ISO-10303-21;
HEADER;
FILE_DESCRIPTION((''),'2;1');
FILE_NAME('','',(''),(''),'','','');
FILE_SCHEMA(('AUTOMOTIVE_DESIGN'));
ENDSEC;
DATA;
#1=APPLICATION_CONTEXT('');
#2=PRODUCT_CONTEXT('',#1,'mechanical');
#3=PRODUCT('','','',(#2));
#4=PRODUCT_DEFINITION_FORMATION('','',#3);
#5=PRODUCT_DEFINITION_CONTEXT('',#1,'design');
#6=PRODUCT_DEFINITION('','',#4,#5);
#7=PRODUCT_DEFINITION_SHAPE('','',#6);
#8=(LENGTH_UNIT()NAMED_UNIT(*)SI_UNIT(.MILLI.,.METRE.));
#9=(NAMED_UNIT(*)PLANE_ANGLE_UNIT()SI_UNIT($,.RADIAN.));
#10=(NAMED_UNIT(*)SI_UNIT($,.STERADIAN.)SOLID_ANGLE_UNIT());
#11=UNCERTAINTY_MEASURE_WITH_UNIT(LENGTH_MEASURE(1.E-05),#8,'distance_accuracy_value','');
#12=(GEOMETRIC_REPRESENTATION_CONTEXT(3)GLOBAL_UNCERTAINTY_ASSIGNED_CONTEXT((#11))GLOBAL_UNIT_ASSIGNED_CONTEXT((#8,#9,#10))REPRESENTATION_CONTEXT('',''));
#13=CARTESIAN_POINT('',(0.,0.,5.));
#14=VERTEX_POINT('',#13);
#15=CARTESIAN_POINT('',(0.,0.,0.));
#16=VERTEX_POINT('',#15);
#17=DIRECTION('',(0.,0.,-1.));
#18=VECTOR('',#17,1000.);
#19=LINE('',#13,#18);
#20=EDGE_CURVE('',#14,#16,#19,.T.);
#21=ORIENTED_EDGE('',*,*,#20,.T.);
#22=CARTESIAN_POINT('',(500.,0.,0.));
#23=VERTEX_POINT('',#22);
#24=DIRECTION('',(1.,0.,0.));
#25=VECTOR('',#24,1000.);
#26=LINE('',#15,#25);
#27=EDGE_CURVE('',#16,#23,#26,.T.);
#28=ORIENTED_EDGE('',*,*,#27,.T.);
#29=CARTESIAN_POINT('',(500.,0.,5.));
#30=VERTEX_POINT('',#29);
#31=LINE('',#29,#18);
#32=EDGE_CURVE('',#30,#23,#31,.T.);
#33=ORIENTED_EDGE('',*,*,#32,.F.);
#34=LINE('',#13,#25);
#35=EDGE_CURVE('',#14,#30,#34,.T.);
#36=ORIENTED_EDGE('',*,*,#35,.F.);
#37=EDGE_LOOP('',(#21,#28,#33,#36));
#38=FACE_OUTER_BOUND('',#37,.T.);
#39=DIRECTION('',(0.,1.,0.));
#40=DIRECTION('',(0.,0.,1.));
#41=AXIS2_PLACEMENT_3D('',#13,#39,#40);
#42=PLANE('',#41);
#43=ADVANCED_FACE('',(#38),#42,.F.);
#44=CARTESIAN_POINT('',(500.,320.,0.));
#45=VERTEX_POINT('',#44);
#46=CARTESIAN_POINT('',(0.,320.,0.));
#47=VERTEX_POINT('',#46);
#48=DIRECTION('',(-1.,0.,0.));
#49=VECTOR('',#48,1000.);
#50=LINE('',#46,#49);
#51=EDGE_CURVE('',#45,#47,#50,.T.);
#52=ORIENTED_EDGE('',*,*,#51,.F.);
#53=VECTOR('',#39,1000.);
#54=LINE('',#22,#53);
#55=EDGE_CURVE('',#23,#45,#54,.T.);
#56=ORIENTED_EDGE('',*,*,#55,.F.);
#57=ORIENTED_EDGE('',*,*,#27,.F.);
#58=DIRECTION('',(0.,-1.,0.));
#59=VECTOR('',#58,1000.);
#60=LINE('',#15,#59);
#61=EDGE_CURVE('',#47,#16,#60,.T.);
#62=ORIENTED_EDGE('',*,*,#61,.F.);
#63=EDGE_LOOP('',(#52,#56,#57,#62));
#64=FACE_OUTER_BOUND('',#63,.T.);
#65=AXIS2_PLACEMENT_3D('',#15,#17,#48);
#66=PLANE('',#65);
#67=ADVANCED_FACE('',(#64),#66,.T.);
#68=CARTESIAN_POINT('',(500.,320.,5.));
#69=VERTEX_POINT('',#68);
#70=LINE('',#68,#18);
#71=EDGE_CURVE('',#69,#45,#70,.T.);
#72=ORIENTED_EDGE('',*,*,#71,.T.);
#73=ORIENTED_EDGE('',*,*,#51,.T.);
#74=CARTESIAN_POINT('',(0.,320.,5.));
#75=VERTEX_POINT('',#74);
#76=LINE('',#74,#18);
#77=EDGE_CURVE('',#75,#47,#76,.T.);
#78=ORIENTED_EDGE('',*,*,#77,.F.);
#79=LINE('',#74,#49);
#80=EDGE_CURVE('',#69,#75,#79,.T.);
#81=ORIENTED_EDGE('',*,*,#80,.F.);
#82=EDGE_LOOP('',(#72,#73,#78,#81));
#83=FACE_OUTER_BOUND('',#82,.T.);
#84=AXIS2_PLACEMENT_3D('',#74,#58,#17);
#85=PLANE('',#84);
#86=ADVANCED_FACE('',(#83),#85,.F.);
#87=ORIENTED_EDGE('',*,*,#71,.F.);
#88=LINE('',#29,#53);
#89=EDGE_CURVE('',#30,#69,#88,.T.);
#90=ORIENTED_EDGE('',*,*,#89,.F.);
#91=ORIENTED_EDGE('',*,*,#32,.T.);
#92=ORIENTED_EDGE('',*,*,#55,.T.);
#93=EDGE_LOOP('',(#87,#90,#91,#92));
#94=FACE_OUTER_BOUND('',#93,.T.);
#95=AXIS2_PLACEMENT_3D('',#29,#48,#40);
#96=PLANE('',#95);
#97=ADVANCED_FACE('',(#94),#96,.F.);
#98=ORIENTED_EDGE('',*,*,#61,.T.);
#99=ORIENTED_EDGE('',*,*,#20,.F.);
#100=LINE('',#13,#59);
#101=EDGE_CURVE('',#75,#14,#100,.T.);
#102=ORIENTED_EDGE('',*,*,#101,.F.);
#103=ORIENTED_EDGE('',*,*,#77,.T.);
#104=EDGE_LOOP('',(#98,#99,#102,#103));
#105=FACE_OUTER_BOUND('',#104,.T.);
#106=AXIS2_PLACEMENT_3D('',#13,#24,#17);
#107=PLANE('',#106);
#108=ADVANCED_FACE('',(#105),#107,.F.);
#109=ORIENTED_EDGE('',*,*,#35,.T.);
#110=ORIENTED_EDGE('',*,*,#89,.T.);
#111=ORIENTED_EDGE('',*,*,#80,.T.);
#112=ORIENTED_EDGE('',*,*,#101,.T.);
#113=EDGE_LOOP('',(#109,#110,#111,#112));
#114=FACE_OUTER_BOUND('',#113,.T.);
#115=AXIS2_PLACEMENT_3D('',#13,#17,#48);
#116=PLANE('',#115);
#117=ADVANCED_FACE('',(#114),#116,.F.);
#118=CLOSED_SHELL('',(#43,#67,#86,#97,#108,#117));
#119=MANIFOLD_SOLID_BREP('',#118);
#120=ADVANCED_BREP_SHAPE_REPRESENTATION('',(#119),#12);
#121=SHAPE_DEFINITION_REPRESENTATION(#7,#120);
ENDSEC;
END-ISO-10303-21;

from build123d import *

# Parameters (mm, degrees)
SKETCH1_W           = 500
SKETCH1_H           = 320
BOSS_EXTRUDE1_DEPTH = 5


with BuildPart() as part:
    # Sketch1 → Boss-Extrude1 (new body)
    with BuildSketch(Plane.XY):
        with Locations((250, 160)):
            Rectangle(SKETCH1_W, SKETCH1_H)
    extrude(amount=BOSS_EXTRUDE1_DEPTH)


solid = part.part
